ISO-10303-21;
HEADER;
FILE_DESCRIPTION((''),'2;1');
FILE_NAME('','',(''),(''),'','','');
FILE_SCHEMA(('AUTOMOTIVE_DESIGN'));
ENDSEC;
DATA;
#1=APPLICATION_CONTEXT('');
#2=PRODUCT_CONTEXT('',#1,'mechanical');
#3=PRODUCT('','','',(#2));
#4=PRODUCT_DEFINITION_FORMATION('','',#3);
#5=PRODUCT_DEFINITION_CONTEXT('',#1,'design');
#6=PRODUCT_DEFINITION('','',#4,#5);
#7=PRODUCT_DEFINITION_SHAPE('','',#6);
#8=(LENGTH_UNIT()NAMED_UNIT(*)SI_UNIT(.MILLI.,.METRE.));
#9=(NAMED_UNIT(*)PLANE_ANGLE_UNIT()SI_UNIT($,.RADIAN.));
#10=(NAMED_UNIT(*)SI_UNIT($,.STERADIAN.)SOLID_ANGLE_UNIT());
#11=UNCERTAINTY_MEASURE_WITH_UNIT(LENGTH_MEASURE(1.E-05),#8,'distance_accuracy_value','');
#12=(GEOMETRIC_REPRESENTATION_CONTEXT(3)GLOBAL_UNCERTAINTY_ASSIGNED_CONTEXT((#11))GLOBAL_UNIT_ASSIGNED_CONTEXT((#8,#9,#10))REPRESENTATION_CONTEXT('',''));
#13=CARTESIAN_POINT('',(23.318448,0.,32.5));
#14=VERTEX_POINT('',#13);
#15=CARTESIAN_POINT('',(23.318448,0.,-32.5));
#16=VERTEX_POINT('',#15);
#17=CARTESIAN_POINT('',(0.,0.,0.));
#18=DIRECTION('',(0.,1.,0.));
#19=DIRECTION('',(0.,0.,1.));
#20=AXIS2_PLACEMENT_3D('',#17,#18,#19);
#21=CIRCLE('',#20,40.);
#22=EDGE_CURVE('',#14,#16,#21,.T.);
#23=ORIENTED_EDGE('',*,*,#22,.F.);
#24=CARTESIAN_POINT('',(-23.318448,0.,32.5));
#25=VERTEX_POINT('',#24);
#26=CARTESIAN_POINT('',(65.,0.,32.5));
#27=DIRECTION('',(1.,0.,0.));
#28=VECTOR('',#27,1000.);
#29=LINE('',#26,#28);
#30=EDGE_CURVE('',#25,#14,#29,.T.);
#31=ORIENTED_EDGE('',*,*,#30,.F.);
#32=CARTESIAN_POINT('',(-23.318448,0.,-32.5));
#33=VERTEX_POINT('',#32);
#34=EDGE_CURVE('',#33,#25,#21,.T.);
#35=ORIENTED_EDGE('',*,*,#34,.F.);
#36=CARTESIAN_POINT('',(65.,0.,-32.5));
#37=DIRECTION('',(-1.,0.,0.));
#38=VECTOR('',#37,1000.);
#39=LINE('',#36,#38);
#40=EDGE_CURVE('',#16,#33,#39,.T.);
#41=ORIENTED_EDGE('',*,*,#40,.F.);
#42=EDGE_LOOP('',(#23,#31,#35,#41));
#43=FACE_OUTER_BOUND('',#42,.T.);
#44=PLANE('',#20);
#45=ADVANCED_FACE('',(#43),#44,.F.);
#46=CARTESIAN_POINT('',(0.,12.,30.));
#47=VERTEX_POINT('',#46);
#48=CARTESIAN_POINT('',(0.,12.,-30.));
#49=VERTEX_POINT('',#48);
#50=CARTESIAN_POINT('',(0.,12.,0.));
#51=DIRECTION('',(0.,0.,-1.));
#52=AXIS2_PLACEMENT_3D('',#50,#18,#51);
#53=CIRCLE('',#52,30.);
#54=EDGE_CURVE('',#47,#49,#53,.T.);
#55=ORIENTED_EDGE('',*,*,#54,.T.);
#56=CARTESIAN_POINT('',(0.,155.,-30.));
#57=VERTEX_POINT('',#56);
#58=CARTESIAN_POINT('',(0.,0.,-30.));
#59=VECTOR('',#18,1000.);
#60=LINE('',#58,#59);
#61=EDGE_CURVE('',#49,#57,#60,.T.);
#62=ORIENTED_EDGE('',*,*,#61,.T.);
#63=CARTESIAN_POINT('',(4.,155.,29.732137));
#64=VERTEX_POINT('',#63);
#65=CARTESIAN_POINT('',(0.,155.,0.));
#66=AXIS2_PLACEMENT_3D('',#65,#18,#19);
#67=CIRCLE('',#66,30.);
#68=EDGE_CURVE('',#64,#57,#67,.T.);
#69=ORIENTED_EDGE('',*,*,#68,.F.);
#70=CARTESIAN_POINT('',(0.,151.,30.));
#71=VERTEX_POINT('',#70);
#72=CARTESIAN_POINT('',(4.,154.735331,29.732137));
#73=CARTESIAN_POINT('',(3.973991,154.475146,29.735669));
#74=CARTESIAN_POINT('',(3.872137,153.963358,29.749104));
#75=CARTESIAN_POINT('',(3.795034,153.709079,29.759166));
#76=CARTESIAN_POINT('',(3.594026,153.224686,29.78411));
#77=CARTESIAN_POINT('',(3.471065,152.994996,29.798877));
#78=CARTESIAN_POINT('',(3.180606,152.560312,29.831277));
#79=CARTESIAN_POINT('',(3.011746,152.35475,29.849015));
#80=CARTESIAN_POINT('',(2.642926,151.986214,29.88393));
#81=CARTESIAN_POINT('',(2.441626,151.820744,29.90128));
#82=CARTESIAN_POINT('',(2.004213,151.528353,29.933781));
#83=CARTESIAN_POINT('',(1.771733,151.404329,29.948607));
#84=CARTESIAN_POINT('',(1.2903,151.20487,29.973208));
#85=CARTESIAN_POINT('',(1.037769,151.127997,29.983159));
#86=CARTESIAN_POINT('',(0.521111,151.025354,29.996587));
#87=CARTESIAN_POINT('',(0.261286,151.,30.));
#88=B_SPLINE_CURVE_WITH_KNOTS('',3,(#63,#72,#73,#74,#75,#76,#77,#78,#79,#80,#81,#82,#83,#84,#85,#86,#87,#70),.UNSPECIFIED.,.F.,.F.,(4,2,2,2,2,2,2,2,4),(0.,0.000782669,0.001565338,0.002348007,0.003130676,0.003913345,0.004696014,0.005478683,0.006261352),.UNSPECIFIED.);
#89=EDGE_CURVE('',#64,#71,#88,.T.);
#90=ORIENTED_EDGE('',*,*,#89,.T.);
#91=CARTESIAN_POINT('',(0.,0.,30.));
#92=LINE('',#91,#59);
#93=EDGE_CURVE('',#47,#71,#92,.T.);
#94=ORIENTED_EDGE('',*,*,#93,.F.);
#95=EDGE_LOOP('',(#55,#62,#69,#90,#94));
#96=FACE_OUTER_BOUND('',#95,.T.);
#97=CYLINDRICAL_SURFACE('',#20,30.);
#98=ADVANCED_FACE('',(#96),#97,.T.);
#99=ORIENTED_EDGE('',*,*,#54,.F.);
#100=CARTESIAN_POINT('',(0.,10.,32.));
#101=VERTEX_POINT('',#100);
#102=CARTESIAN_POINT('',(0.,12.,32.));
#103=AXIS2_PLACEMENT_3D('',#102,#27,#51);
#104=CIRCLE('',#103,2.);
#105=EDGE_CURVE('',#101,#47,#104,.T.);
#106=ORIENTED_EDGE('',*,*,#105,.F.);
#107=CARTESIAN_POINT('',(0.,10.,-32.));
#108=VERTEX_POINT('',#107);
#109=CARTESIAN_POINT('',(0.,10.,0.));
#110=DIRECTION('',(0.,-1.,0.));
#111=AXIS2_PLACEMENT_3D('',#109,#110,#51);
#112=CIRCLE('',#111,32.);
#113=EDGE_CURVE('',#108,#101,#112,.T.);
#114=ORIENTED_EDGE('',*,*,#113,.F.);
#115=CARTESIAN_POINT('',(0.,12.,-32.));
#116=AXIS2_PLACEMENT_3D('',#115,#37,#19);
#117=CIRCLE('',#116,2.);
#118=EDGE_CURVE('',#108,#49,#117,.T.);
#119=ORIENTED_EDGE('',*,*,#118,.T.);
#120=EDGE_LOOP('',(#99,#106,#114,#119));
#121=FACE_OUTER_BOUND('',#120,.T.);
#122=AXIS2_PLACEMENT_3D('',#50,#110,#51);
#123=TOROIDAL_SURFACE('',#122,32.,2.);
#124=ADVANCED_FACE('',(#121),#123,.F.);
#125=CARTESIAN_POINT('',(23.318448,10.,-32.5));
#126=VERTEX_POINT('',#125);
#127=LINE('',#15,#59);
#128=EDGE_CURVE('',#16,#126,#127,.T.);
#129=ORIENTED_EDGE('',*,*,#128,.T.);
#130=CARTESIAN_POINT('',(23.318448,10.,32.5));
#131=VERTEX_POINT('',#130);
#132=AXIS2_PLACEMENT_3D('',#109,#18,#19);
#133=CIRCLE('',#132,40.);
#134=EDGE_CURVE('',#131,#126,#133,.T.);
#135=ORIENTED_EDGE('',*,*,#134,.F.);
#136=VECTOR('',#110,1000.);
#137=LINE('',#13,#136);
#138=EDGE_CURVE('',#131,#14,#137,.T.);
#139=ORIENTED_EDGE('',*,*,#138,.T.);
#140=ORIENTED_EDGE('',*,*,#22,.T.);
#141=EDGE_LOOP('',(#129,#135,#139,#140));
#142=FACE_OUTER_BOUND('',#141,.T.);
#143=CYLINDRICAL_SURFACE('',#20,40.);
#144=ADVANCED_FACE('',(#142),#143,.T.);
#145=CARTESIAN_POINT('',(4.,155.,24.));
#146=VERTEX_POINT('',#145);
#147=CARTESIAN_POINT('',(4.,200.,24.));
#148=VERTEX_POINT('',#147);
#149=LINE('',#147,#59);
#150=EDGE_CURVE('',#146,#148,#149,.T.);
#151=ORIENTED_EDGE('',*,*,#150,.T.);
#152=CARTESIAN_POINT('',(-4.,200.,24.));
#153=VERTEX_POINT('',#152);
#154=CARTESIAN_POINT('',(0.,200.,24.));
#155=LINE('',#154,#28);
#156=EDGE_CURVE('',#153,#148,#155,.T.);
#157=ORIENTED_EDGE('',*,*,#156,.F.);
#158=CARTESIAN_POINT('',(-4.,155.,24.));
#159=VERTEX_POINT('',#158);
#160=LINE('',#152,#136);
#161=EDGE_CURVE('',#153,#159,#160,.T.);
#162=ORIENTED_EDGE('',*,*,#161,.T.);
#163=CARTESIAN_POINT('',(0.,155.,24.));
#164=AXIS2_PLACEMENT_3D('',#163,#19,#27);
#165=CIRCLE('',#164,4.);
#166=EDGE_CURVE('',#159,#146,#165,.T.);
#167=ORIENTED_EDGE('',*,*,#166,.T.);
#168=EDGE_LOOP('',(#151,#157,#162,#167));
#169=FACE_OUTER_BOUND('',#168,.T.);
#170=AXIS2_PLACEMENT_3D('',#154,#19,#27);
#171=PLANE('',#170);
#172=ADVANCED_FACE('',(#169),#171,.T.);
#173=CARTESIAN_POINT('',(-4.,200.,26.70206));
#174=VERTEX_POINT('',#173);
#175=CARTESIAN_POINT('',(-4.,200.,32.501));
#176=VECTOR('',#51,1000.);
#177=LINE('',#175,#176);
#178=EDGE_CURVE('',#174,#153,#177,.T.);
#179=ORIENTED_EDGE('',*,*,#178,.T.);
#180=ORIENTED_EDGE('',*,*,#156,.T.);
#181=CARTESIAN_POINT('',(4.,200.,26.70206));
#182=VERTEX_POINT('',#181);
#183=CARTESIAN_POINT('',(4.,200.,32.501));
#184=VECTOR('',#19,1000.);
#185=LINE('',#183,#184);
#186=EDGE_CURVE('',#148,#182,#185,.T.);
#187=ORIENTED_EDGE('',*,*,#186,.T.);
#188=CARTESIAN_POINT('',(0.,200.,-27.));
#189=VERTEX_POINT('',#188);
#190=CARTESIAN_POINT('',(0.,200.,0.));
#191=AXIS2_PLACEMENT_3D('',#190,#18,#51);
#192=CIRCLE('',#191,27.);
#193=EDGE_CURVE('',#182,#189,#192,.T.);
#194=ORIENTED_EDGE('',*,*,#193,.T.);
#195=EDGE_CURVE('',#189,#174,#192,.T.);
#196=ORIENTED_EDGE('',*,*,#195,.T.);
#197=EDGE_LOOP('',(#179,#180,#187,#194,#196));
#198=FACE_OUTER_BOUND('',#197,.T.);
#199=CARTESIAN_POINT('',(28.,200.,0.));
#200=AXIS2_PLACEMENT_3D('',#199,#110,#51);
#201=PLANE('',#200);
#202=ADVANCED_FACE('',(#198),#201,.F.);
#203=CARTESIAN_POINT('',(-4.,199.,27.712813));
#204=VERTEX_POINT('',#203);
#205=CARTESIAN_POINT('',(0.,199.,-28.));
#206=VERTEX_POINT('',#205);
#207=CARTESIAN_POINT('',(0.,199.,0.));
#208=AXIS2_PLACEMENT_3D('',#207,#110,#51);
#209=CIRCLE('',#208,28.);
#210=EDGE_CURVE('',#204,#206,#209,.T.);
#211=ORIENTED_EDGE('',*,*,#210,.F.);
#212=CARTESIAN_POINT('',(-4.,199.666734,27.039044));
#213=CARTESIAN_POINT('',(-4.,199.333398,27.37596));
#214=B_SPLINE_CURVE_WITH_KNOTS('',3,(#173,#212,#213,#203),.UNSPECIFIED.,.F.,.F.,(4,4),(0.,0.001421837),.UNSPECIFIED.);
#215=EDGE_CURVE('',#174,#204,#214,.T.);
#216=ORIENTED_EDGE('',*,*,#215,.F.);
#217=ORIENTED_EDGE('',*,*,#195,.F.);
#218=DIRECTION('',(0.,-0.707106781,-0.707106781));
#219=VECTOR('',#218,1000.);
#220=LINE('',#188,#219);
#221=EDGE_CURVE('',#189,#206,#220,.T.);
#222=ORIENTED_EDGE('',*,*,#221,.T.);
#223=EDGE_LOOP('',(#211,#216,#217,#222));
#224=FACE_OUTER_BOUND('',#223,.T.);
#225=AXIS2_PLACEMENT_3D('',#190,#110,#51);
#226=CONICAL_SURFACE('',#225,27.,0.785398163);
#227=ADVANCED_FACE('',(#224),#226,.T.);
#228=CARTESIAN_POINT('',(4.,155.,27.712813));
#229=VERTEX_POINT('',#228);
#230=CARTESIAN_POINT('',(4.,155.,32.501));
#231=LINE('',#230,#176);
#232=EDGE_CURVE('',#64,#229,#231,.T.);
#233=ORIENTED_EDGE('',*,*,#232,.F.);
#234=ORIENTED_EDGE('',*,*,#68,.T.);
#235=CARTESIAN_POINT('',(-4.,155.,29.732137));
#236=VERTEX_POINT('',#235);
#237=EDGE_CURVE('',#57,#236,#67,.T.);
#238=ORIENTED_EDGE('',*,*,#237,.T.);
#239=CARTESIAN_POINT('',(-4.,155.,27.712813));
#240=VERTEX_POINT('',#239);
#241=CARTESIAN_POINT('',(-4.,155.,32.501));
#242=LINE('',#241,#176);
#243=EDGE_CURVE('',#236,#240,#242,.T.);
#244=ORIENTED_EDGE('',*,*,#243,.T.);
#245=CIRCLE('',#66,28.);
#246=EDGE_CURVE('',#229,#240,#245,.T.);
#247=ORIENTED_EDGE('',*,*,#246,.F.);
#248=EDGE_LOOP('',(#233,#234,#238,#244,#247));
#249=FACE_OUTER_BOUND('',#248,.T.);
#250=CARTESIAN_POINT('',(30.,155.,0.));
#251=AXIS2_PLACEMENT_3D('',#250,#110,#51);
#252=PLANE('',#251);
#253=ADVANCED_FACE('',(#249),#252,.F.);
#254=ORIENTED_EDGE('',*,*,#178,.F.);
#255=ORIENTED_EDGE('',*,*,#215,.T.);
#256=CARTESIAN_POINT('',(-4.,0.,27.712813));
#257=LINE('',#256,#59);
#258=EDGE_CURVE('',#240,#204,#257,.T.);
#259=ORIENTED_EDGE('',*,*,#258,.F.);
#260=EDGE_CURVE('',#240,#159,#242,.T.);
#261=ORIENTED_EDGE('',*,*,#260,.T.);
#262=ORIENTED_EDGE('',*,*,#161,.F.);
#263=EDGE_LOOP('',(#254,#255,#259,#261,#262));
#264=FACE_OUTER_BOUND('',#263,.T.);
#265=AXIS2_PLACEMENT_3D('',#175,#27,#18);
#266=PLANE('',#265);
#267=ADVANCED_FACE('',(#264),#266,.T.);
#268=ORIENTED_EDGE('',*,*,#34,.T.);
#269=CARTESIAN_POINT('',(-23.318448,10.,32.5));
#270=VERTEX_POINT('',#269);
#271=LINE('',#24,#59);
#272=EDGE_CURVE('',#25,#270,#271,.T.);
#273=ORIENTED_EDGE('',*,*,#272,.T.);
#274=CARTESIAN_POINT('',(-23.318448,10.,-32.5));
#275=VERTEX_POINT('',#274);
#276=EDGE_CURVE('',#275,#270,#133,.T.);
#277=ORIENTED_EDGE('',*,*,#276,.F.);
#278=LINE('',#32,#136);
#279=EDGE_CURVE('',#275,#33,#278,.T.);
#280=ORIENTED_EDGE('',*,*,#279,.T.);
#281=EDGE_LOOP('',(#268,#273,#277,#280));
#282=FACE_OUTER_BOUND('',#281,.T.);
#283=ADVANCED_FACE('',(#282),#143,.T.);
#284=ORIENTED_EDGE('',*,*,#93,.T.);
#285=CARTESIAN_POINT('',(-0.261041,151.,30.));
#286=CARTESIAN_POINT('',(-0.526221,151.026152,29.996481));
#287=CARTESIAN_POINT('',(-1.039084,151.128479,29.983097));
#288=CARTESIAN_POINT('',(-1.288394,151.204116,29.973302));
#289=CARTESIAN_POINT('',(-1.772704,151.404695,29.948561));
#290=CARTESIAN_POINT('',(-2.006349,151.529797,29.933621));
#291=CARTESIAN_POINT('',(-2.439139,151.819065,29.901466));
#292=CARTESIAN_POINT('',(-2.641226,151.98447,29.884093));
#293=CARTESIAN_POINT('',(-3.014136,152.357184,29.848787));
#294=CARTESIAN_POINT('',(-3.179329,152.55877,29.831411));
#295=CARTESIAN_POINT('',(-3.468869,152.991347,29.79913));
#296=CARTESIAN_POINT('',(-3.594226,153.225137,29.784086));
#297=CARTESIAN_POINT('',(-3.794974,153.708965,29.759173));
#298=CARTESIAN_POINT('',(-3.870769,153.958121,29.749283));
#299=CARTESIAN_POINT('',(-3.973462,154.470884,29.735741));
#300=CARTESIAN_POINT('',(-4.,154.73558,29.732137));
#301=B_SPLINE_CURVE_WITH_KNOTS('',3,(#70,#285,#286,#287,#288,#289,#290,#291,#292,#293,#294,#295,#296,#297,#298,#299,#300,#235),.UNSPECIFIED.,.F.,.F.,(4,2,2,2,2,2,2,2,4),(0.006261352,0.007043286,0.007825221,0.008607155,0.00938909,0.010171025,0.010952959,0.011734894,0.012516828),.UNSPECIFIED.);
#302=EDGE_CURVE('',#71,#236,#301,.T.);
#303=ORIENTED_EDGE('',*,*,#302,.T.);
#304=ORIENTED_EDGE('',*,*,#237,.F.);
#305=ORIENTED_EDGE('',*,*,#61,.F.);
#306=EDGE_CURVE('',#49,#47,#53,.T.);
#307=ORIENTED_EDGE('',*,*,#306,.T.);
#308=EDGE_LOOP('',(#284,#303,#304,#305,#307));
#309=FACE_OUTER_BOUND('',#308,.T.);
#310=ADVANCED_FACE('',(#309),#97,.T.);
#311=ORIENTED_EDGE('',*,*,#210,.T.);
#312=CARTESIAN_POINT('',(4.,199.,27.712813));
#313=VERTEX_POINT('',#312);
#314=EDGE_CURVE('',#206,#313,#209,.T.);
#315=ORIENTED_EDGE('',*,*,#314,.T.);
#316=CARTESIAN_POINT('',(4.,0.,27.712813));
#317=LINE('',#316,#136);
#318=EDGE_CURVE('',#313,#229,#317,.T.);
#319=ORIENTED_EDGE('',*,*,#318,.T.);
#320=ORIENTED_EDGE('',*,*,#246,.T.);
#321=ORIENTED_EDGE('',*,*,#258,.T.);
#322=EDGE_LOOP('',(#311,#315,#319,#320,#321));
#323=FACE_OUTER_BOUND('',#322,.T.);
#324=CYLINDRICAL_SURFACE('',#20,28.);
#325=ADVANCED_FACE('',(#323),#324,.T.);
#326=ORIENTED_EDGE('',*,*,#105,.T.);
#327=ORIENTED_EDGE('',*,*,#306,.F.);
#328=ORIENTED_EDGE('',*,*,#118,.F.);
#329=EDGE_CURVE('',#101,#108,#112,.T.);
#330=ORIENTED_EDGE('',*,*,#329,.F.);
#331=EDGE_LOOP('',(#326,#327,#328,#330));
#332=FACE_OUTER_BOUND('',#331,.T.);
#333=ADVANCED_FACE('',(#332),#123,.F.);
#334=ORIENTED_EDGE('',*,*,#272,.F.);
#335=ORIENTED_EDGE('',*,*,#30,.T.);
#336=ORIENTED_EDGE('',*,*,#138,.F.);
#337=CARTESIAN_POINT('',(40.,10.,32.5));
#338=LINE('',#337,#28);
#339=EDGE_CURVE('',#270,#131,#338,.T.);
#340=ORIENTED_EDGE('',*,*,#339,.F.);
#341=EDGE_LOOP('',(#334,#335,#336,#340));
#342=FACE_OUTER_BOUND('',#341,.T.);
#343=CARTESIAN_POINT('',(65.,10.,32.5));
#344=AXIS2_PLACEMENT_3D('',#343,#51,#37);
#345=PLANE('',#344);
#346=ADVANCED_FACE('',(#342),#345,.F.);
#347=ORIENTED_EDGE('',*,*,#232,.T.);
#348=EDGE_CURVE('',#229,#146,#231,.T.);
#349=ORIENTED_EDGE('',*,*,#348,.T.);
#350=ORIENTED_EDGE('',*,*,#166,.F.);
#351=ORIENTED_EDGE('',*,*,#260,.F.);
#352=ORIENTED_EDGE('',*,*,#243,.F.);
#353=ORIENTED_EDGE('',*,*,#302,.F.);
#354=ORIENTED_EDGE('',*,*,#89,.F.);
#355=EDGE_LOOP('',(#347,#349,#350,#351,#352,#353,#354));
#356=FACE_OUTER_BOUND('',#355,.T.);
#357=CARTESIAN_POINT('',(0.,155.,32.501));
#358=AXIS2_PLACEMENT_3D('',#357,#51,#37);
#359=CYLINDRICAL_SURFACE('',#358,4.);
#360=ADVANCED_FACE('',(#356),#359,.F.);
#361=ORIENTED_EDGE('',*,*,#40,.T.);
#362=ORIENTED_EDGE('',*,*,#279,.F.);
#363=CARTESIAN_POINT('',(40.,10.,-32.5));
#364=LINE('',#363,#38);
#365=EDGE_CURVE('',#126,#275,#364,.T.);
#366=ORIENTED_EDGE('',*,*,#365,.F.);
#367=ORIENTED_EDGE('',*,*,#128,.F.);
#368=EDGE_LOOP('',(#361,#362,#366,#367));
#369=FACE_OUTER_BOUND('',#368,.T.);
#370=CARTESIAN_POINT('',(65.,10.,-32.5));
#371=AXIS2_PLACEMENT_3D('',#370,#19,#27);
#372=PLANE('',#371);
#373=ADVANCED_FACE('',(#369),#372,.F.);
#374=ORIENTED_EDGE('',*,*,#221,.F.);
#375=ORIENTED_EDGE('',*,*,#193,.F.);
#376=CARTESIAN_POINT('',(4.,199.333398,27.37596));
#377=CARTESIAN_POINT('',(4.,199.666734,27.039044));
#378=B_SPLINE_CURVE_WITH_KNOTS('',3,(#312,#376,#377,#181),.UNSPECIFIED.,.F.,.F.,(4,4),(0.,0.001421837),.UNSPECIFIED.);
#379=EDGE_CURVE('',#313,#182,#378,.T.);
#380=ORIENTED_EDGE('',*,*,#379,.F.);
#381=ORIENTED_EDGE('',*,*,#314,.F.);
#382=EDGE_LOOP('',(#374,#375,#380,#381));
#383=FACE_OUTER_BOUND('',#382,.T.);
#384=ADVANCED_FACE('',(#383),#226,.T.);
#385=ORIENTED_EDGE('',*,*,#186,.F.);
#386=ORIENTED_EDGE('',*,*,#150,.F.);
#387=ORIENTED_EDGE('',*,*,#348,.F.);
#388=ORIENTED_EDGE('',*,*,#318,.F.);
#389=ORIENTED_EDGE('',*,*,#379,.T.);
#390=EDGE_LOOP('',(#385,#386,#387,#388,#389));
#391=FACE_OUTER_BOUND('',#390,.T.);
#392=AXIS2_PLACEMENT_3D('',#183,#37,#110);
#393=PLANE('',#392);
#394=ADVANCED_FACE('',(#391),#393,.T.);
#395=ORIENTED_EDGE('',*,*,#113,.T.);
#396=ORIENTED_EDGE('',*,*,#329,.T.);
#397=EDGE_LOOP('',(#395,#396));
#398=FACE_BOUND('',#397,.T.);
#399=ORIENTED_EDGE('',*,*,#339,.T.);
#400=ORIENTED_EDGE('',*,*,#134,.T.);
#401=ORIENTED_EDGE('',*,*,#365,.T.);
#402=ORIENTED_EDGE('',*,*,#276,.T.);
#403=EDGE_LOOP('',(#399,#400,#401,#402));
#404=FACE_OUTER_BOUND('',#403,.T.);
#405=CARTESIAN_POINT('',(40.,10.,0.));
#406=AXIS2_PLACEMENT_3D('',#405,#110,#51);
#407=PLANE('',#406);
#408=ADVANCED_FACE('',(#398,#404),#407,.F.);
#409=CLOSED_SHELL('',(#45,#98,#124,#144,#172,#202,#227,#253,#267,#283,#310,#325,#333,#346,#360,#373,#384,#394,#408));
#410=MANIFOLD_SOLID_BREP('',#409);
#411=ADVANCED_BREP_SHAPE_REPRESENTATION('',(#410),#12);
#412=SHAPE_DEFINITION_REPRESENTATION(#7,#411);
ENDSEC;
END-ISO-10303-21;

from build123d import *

# Parameters (mm, degrees)
SKETCH2_OUTSIDE_W   = 127.956
SKETCH2_OUTSIDE_H   = 127.956
SKETCH2_OUTSIDE_W_2 = 130
SKETCH2_OUTSIDE_H_2 = 65
CUT_EXTRUDE1_DEPTH  = 10
CUT_EXTRUDE2_REACH  = 213.642
CHAMFER1_SIZE       = 1
FILLET2_R           = 2


with BuildPart() as part:
    # Sketch1 → Revolve1 (revolve)
    with BuildSketch(Plane.XY, mode=Mode.PRIVATE) as revolve1_sk:
        Polygon((0, 0), (40, 0), (40, 10), (30, 10), (30, 155), (28, 155), (28, 200), (0, 200), align=None)
    revolve(revolve1_sk.sketch.rotate(Axis((0, 0, 0), (0, -1, 0)), 90), axis=Axis((0, 0, 0), (0, -1, 0)))

    # Sketch2 outside → Cut-Extrude1 (cut)
    with BuildSketch(Plane(origin=(0, 0, 0), x_dir=(1, 0, 0), z_dir=(0, 1, 0))):
        Rectangle(SKETCH2_OUTSIDE_W, SKETCH2_OUTSIDE_H)
        Rectangle(SKETCH2_OUTSIDE_W_2, SKETCH2_OUTSIDE_H_2, mode=Mode.SUBTRACT)
    extrude(amount=CUT_EXTRUDE1_DEPTH, mode=Mode.SUBTRACT)

    # Sketch3 → Cut-Extrude2 (cut, up to next)
    with BuildSketch(Plane.XY.offset(24), mode=Mode.PRIVATE) as cut_extrude2_sk1:
        with BuildLine():
            Line((4, 200), (4, 155))
            ThreePointArc((4, 155), (0, 151), (-4, 155))
            Line((-4, 155), (-4, 200))
            ThreePointArc((-4, 200), (0, 204), (4, 200))
        make_face()
    cut_extrude2_tool1 = extrude(cut_extrude2_sk1.sketch, amount=CUT_EXTRUDE2_REACH, mode=Mode.PRIVATE) & part.part
    add(cut_extrude2_tool1.solids().sort_by_distance((0, 177.5, 24))[0], mode=Mode.SUBTRACT)

    # Chamfer1
    chamfer1_edges = [part.edges().sort_by_distance(p)[0] for p in [
        (0, 200, -28),
    ]]
    chamfer(chamfer1_edges, length=CHAMFER1_SIZE)

    # Fillet2
    fillet2_edges = [part.edges().sort_by_distance(p)[0] for p in [
        (0, 10, -30),
    ]]
    fillet(fillet2_edges, radius=FILLET2_R)


solid = part.part
